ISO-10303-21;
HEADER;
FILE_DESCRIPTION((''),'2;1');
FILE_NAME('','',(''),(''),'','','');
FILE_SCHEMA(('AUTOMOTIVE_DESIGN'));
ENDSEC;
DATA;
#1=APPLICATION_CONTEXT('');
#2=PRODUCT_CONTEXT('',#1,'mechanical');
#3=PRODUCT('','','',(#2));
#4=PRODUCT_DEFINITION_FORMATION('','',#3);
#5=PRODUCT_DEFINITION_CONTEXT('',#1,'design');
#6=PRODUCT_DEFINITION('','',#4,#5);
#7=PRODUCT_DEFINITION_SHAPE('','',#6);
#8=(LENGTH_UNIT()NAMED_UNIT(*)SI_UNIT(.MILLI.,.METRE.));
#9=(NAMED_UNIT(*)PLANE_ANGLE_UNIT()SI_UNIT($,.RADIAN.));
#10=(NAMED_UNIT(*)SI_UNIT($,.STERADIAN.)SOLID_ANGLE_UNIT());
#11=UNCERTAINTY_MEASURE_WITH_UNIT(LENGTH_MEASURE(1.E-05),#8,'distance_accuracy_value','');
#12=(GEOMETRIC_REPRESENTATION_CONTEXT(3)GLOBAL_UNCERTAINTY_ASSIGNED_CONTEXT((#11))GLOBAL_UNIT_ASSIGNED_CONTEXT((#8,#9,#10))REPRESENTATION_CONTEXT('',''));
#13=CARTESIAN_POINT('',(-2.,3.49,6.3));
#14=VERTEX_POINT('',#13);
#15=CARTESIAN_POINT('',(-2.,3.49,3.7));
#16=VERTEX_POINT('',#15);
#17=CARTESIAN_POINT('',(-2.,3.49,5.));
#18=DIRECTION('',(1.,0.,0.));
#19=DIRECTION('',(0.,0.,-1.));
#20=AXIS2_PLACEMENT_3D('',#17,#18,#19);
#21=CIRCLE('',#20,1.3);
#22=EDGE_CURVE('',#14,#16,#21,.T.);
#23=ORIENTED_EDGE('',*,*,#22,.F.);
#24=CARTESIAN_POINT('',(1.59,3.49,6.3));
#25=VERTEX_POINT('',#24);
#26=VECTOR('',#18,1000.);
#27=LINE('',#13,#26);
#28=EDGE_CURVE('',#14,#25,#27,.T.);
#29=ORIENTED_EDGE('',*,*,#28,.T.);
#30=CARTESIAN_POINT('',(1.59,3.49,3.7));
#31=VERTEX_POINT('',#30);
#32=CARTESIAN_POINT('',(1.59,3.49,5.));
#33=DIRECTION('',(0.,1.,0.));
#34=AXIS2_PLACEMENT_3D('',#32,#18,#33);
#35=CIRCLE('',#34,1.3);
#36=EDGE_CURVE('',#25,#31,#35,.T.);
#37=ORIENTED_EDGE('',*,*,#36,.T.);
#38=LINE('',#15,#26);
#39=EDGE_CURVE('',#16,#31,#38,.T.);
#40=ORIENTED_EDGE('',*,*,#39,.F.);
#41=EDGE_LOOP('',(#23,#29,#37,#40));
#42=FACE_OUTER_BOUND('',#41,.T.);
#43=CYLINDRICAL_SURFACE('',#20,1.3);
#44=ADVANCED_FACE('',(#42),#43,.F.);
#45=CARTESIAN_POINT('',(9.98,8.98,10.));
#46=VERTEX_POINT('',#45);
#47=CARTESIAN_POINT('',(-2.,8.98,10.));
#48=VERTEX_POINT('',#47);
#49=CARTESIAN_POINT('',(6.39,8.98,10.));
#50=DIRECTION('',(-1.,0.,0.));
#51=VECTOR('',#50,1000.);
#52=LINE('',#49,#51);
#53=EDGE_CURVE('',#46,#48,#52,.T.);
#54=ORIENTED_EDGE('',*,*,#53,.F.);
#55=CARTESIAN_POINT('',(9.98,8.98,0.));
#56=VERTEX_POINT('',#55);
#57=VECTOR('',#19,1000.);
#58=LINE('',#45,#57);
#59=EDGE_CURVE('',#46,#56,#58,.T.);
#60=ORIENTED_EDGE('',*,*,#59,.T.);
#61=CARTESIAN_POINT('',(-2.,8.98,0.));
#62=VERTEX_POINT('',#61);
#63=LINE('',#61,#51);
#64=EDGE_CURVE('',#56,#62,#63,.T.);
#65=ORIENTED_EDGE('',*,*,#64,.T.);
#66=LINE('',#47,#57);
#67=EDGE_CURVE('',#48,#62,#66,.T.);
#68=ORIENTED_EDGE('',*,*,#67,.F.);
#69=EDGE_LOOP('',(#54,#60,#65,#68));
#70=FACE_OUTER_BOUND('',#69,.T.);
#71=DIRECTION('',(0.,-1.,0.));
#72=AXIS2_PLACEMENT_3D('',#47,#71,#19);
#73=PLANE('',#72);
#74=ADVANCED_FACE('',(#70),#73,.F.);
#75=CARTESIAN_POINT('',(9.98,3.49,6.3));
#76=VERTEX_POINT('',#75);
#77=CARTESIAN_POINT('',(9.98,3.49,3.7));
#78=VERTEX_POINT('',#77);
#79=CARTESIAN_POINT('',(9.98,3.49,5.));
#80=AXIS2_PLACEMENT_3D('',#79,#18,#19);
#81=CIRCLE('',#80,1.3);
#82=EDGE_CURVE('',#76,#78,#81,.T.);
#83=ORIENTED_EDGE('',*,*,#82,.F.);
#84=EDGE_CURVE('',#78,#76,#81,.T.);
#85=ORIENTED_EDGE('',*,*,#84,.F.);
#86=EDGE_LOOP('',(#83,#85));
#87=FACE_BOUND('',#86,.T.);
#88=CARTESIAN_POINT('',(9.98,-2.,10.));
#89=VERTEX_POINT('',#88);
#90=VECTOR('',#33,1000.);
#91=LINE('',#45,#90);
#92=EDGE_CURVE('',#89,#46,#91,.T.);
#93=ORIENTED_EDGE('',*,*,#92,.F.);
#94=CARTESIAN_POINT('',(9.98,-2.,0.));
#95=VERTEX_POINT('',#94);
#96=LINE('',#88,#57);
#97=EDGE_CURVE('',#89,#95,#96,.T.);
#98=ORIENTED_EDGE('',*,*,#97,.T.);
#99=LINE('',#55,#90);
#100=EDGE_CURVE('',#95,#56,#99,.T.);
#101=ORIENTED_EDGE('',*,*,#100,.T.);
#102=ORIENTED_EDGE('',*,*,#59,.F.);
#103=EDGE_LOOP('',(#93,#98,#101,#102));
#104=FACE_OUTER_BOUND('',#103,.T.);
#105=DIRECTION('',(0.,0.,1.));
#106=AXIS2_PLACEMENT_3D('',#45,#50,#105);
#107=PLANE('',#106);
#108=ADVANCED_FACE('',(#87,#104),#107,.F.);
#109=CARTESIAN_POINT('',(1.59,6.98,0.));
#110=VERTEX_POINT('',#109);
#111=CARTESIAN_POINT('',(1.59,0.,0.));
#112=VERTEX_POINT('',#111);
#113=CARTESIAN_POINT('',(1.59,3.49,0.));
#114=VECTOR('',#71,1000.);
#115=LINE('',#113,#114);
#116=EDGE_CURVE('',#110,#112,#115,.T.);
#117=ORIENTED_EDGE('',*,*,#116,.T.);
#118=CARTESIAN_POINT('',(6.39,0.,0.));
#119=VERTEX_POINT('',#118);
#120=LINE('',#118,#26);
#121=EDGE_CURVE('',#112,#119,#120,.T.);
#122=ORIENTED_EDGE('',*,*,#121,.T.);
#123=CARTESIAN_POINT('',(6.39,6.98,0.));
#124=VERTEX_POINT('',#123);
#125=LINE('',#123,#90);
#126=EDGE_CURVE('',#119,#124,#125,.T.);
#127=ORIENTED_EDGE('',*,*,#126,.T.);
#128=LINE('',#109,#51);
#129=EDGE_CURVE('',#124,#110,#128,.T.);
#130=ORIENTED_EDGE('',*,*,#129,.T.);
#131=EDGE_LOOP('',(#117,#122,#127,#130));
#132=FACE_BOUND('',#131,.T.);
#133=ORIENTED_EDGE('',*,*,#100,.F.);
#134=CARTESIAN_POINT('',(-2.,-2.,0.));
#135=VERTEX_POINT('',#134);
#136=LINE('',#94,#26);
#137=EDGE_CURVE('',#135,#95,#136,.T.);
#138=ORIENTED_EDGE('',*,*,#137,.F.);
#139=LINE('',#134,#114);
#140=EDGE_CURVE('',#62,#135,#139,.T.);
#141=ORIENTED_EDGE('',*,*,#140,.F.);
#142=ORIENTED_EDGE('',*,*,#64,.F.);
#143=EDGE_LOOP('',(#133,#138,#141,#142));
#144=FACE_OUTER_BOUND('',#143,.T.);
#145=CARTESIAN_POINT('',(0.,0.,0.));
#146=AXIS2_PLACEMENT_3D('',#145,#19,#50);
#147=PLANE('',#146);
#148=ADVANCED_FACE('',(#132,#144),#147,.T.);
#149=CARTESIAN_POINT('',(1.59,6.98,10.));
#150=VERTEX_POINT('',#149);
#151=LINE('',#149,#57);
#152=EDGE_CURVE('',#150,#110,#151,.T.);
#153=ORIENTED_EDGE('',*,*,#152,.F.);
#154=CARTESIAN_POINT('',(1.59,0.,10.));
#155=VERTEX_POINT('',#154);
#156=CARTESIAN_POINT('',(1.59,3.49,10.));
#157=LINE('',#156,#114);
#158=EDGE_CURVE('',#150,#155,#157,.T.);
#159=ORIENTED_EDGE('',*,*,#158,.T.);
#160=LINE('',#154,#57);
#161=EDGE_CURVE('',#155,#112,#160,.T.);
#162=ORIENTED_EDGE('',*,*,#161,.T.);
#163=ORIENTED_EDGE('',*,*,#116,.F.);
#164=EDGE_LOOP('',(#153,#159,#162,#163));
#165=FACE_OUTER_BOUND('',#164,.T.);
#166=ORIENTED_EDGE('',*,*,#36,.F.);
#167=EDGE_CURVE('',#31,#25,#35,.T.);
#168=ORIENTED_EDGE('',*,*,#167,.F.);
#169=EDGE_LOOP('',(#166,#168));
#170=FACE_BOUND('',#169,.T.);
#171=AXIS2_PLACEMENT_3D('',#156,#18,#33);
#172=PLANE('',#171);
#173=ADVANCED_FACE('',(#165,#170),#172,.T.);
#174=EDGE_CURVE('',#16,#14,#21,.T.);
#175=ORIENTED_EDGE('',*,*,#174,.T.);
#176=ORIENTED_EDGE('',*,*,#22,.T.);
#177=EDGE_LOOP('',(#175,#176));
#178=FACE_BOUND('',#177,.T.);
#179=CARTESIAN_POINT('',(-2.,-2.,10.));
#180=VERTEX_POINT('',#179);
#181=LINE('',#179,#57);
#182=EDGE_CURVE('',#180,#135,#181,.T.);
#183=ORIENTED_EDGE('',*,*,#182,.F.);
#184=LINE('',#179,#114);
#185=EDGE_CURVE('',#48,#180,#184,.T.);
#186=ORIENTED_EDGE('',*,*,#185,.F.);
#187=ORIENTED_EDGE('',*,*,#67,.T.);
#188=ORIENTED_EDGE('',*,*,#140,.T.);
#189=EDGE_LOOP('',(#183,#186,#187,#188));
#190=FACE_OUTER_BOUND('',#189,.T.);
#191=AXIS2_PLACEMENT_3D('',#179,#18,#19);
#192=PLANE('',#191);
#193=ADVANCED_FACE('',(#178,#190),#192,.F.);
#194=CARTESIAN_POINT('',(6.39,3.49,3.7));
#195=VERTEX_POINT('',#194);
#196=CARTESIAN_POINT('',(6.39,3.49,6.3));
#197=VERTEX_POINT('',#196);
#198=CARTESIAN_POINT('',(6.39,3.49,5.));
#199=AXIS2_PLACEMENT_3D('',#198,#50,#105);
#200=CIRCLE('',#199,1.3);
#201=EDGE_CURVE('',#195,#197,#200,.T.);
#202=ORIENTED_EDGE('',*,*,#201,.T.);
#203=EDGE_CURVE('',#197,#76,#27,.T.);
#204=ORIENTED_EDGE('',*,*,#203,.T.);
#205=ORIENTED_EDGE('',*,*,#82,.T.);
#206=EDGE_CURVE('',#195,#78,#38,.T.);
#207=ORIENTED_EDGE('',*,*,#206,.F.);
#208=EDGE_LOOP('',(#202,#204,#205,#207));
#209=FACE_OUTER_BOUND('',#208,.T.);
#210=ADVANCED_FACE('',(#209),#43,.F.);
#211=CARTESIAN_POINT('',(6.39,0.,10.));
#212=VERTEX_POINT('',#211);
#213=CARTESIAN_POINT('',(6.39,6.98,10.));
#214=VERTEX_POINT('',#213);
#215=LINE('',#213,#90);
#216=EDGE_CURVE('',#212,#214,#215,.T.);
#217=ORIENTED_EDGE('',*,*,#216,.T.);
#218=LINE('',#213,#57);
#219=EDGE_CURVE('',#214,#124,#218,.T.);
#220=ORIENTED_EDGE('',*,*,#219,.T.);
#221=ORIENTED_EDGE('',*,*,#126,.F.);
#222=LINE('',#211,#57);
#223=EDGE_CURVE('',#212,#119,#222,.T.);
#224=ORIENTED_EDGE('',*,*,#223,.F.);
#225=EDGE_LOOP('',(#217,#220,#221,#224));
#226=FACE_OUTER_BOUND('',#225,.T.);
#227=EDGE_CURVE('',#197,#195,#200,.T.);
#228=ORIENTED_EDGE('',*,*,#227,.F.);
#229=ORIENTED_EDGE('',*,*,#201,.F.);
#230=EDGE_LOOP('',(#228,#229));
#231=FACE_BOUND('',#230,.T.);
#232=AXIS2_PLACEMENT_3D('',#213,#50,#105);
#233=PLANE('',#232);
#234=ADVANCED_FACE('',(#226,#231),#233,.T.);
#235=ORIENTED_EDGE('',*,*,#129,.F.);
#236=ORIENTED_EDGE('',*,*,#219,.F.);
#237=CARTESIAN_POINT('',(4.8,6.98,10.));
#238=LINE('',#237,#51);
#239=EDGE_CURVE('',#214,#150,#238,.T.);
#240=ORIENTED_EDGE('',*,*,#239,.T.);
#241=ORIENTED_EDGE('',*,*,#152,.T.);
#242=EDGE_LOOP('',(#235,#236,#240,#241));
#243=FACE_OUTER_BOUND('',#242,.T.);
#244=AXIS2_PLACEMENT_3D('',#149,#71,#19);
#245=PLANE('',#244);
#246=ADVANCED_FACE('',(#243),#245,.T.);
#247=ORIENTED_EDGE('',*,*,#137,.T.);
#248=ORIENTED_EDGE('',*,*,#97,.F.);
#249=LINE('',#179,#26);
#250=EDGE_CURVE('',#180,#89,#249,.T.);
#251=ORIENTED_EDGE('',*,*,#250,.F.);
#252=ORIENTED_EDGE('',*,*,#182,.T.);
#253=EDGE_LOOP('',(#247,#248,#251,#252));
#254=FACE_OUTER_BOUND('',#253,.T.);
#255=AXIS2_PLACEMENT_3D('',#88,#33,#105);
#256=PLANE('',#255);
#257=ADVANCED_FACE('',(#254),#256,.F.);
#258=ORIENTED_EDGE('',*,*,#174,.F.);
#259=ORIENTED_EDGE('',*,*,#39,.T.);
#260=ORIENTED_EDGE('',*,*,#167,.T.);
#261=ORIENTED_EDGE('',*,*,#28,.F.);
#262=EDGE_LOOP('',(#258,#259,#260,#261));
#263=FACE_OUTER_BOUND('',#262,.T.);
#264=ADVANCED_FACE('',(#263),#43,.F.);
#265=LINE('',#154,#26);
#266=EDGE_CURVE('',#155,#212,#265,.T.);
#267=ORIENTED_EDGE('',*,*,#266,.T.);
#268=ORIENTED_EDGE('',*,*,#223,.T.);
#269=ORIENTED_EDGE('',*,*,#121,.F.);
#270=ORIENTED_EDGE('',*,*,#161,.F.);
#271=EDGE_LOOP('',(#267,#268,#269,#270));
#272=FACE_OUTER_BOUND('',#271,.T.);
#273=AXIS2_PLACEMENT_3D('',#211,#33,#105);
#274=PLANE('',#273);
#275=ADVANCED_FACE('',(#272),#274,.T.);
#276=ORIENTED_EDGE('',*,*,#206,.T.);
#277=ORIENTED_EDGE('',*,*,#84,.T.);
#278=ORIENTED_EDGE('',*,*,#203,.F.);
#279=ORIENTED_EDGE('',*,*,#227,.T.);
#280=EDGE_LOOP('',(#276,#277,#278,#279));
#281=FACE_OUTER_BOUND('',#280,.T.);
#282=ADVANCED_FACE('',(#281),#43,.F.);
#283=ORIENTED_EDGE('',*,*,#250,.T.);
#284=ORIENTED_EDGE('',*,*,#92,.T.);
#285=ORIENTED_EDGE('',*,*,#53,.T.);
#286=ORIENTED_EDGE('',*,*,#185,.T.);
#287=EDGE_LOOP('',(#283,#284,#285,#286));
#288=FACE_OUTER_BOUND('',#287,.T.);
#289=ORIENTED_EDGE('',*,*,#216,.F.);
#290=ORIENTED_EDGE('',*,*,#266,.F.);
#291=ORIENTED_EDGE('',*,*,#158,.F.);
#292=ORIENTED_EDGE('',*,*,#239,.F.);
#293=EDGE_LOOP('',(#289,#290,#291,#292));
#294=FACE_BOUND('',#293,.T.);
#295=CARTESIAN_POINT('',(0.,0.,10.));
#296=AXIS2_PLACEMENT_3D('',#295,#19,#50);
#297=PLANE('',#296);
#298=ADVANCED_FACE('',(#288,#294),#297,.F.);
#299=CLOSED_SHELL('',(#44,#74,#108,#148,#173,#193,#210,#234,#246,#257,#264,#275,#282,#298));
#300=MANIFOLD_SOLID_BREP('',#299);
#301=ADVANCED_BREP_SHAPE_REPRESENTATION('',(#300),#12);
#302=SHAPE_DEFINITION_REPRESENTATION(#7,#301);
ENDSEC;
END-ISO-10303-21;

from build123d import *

# Parameters (mm, degrees)
BOSS_EXTRUDE1_DEPTH = 10
SKETCH4_R           = 1.3
CUT_EXTRUDE2_DEPTH  = 19.004466113


with BuildPart() as part:
    # Sketch1 → Boss-Extrude1 (new body)
    with BuildSketch(Plane.XY):
        Polygon((-2, 8.98), (6.39, 8.98), (9.98, 8.98), (9.98, -2), (6.39, -2), (-2, -2), align=None)
        Polygon((1.59, 0), (4.8, 0), (6.39, 0), (6.39, 6.98), (4.8, 6.98), (1.59, 6.98), (1.59, 3.49), align=None, mode=Mode.SUBTRACT)
    extrude(amount=BOSS_EXTRUDE1_DEPTH)

    # Sketch4 → Cut-Extrude2 (cut, through all)
    with BuildSketch(Plane(origin=(9.98, 0, 0), x_dir=(0, 0, -1), z_dir=(1, 0, 0))):
        with Locations((-5, 3.49)):
            Circle(SKETCH4_R)
    extrude(amount=-CUT_EXTRUDE2_DEPTH, mode=Mode.SUBTRACT)


solid = part.part
